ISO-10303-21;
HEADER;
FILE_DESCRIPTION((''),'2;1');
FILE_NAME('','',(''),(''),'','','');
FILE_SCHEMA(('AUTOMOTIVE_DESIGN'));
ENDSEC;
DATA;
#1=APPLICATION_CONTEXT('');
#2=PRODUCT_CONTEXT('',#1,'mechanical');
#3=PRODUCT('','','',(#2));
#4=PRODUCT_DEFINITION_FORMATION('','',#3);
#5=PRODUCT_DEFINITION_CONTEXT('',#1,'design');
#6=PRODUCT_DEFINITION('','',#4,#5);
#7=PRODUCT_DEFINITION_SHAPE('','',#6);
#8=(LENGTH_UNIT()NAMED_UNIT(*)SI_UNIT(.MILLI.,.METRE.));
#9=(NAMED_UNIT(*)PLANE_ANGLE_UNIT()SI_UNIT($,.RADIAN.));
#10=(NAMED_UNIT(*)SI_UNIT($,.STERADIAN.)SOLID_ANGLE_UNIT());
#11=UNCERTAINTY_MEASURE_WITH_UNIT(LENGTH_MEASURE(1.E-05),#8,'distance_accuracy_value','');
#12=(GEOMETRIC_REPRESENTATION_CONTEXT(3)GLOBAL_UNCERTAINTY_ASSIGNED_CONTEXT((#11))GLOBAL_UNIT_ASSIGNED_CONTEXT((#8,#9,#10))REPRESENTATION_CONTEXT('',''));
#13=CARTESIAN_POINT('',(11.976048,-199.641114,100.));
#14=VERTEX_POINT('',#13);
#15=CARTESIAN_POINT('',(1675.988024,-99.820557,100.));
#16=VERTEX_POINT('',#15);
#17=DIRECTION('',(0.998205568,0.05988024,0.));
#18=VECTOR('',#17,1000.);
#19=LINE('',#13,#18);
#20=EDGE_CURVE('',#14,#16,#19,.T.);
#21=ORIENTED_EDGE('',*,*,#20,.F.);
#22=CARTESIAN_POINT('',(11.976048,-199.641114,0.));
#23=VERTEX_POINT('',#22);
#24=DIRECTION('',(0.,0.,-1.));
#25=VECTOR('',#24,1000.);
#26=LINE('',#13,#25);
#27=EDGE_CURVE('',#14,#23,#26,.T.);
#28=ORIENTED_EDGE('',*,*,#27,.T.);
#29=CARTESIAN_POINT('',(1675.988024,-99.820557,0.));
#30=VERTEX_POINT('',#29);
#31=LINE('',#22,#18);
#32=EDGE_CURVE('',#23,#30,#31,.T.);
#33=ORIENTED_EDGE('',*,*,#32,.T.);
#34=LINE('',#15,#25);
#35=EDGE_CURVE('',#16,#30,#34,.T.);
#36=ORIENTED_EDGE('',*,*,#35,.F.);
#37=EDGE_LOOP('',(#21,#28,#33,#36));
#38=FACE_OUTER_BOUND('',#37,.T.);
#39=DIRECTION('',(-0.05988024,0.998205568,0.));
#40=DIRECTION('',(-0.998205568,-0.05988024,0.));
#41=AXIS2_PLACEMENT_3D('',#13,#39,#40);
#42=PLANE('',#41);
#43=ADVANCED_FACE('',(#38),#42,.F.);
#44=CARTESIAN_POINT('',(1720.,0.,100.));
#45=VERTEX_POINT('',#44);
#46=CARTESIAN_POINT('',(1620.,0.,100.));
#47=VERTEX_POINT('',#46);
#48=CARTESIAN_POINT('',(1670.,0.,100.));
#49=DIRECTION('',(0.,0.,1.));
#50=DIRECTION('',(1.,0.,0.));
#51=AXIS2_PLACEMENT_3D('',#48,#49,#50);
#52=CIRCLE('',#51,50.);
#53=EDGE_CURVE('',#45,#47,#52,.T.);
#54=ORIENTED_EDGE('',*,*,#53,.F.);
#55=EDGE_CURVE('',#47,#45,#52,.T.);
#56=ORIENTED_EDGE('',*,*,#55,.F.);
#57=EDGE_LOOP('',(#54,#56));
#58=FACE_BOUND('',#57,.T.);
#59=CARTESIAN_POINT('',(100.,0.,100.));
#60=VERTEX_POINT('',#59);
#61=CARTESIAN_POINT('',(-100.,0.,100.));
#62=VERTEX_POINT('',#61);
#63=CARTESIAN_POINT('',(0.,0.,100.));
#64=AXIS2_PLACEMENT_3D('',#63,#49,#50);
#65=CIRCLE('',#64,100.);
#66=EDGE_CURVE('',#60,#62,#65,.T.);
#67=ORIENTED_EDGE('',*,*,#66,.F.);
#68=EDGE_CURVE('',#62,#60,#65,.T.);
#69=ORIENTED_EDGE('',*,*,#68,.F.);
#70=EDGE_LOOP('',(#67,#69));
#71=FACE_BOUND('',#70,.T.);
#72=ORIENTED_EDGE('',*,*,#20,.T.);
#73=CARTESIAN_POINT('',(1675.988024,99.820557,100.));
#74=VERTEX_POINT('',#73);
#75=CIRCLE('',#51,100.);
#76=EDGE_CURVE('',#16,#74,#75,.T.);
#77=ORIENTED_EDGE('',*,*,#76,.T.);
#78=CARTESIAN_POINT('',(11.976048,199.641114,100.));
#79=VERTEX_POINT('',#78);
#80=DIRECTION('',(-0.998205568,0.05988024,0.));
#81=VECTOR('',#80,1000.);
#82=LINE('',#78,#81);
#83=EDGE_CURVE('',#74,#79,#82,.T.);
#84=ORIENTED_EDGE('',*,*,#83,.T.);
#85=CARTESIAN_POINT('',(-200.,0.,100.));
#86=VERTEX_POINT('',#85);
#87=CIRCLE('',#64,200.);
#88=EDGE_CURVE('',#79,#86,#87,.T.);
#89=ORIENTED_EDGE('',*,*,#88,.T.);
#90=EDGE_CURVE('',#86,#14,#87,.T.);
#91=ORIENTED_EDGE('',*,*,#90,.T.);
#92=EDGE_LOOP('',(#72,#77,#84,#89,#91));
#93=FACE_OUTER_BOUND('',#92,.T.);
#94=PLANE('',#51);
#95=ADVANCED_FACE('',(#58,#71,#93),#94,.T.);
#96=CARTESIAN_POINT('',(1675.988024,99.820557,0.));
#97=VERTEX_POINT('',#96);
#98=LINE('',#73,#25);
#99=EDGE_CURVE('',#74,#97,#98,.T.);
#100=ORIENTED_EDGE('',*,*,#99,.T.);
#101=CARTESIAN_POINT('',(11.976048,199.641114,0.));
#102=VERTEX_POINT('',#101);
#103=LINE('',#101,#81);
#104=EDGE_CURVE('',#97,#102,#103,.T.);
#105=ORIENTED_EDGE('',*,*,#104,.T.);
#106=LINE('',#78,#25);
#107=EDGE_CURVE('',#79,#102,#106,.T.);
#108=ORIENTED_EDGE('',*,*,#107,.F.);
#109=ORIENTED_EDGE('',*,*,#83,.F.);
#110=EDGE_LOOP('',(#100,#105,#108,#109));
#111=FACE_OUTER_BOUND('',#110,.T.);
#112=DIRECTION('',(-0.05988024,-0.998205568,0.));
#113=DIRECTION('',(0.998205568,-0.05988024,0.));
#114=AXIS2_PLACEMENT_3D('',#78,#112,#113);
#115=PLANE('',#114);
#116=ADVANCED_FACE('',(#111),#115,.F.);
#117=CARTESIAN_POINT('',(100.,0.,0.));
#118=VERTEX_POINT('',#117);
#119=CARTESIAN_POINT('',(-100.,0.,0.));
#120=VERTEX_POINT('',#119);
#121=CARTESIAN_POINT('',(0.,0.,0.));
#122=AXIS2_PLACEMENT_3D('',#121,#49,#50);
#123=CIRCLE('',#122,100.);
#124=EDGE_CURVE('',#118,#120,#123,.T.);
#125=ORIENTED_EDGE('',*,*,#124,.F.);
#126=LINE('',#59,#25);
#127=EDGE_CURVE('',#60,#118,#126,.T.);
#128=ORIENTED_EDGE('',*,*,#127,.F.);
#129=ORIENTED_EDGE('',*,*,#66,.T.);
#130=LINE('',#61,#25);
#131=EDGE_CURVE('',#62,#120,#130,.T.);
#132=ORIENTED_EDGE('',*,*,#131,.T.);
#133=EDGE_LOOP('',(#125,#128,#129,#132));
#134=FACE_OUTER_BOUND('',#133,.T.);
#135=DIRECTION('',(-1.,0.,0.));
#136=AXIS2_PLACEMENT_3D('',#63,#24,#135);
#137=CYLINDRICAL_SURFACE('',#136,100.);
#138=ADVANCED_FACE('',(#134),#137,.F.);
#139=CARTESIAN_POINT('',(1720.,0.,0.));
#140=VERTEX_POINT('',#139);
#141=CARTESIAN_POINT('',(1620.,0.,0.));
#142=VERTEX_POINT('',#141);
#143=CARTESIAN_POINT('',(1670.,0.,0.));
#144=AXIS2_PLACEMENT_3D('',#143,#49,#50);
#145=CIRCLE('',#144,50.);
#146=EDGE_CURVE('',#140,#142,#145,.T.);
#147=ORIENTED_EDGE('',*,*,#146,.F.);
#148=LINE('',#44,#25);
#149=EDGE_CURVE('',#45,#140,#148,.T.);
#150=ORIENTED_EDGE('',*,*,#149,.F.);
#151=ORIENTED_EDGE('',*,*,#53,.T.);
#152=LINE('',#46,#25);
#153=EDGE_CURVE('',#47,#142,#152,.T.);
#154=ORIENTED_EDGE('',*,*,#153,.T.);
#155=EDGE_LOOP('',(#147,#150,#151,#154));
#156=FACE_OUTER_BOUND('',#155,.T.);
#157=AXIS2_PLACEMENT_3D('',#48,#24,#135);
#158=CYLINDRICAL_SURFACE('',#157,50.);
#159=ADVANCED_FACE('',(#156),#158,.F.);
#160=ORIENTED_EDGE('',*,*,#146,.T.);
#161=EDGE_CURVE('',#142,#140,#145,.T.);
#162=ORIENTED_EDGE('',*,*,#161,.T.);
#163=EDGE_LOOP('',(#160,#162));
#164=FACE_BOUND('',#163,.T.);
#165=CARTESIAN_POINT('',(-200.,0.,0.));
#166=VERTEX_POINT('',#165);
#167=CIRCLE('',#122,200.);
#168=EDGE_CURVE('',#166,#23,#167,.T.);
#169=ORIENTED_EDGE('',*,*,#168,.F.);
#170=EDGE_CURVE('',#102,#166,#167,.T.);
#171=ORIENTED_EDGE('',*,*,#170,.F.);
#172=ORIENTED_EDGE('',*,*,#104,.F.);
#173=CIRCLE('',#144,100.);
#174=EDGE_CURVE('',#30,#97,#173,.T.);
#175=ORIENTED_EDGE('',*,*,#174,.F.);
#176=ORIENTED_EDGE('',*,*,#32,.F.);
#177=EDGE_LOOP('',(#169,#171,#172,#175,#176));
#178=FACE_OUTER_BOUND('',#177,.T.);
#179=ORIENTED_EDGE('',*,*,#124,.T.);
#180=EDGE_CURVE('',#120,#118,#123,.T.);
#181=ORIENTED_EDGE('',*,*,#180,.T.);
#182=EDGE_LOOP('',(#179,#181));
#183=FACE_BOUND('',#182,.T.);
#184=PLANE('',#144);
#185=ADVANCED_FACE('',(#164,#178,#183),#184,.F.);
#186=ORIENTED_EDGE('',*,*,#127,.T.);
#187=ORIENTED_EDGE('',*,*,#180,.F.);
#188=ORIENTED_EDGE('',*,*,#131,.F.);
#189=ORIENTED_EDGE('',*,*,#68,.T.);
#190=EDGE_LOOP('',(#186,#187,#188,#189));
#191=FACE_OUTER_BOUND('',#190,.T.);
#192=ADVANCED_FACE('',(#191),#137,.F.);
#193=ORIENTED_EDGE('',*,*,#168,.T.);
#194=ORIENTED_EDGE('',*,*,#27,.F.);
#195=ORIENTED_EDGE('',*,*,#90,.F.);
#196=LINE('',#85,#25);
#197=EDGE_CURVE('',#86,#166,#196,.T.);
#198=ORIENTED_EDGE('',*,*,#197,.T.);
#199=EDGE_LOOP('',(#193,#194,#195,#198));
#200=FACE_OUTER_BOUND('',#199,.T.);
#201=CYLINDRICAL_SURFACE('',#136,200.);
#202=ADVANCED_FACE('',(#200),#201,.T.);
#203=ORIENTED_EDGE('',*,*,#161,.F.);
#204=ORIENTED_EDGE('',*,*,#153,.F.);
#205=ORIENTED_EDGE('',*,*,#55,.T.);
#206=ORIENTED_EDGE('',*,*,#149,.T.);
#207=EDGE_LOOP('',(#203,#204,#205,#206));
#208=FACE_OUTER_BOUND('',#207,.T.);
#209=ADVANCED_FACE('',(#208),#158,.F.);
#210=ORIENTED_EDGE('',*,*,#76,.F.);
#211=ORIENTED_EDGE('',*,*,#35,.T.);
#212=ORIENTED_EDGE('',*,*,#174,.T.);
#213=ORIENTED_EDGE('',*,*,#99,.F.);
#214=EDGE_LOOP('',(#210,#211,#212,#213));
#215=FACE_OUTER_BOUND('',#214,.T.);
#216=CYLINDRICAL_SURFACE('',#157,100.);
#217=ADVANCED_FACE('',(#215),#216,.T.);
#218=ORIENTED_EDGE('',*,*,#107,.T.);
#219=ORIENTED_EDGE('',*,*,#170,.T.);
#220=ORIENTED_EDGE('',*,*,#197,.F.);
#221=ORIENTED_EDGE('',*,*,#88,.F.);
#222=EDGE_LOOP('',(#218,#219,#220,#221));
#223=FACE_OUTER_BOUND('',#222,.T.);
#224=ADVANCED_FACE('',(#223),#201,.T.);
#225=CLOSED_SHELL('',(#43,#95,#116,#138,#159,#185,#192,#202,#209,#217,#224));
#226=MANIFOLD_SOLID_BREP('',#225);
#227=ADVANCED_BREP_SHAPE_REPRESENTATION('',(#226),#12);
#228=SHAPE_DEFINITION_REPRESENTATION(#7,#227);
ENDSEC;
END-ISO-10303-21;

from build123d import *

# Parameters (mm, degrees)
SKETCH1_R           = 100
SKETCH1_R_2         = 50
BOSS_EXTRUDE1_DEPTH = 100


with BuildPart() as part:
    # Sketch1 → Boss-Extrude1 (new body)
    with BuildSketch(Plane.XY):
        with BuildLine():
            Line((11.976047904, 199.641113693), (1675.988023952, 99.820556847))
            ThreePointArc((1675.988023952, 99.820556847), (1770, 0), (1675.988023952, -99.820556847))
            Line((1675.988023952, -99.820556847), (11.976047904, -199.641113693))
            ThreePointArc((11.976047904, -199.641113693), (-200, 0), (11.976047904, 199.641113693))
        make_face()
        Circle(SKETCH1_R, mode=Mode.SUBTRACT)
        with Locations((1670, 0)):
            Circle(SKETCH1_R_2, mode=Mode.SUBTRACT)
    extrude(amount=BOSS_EXTRUDE1_DEPTH)


solid = part.part
